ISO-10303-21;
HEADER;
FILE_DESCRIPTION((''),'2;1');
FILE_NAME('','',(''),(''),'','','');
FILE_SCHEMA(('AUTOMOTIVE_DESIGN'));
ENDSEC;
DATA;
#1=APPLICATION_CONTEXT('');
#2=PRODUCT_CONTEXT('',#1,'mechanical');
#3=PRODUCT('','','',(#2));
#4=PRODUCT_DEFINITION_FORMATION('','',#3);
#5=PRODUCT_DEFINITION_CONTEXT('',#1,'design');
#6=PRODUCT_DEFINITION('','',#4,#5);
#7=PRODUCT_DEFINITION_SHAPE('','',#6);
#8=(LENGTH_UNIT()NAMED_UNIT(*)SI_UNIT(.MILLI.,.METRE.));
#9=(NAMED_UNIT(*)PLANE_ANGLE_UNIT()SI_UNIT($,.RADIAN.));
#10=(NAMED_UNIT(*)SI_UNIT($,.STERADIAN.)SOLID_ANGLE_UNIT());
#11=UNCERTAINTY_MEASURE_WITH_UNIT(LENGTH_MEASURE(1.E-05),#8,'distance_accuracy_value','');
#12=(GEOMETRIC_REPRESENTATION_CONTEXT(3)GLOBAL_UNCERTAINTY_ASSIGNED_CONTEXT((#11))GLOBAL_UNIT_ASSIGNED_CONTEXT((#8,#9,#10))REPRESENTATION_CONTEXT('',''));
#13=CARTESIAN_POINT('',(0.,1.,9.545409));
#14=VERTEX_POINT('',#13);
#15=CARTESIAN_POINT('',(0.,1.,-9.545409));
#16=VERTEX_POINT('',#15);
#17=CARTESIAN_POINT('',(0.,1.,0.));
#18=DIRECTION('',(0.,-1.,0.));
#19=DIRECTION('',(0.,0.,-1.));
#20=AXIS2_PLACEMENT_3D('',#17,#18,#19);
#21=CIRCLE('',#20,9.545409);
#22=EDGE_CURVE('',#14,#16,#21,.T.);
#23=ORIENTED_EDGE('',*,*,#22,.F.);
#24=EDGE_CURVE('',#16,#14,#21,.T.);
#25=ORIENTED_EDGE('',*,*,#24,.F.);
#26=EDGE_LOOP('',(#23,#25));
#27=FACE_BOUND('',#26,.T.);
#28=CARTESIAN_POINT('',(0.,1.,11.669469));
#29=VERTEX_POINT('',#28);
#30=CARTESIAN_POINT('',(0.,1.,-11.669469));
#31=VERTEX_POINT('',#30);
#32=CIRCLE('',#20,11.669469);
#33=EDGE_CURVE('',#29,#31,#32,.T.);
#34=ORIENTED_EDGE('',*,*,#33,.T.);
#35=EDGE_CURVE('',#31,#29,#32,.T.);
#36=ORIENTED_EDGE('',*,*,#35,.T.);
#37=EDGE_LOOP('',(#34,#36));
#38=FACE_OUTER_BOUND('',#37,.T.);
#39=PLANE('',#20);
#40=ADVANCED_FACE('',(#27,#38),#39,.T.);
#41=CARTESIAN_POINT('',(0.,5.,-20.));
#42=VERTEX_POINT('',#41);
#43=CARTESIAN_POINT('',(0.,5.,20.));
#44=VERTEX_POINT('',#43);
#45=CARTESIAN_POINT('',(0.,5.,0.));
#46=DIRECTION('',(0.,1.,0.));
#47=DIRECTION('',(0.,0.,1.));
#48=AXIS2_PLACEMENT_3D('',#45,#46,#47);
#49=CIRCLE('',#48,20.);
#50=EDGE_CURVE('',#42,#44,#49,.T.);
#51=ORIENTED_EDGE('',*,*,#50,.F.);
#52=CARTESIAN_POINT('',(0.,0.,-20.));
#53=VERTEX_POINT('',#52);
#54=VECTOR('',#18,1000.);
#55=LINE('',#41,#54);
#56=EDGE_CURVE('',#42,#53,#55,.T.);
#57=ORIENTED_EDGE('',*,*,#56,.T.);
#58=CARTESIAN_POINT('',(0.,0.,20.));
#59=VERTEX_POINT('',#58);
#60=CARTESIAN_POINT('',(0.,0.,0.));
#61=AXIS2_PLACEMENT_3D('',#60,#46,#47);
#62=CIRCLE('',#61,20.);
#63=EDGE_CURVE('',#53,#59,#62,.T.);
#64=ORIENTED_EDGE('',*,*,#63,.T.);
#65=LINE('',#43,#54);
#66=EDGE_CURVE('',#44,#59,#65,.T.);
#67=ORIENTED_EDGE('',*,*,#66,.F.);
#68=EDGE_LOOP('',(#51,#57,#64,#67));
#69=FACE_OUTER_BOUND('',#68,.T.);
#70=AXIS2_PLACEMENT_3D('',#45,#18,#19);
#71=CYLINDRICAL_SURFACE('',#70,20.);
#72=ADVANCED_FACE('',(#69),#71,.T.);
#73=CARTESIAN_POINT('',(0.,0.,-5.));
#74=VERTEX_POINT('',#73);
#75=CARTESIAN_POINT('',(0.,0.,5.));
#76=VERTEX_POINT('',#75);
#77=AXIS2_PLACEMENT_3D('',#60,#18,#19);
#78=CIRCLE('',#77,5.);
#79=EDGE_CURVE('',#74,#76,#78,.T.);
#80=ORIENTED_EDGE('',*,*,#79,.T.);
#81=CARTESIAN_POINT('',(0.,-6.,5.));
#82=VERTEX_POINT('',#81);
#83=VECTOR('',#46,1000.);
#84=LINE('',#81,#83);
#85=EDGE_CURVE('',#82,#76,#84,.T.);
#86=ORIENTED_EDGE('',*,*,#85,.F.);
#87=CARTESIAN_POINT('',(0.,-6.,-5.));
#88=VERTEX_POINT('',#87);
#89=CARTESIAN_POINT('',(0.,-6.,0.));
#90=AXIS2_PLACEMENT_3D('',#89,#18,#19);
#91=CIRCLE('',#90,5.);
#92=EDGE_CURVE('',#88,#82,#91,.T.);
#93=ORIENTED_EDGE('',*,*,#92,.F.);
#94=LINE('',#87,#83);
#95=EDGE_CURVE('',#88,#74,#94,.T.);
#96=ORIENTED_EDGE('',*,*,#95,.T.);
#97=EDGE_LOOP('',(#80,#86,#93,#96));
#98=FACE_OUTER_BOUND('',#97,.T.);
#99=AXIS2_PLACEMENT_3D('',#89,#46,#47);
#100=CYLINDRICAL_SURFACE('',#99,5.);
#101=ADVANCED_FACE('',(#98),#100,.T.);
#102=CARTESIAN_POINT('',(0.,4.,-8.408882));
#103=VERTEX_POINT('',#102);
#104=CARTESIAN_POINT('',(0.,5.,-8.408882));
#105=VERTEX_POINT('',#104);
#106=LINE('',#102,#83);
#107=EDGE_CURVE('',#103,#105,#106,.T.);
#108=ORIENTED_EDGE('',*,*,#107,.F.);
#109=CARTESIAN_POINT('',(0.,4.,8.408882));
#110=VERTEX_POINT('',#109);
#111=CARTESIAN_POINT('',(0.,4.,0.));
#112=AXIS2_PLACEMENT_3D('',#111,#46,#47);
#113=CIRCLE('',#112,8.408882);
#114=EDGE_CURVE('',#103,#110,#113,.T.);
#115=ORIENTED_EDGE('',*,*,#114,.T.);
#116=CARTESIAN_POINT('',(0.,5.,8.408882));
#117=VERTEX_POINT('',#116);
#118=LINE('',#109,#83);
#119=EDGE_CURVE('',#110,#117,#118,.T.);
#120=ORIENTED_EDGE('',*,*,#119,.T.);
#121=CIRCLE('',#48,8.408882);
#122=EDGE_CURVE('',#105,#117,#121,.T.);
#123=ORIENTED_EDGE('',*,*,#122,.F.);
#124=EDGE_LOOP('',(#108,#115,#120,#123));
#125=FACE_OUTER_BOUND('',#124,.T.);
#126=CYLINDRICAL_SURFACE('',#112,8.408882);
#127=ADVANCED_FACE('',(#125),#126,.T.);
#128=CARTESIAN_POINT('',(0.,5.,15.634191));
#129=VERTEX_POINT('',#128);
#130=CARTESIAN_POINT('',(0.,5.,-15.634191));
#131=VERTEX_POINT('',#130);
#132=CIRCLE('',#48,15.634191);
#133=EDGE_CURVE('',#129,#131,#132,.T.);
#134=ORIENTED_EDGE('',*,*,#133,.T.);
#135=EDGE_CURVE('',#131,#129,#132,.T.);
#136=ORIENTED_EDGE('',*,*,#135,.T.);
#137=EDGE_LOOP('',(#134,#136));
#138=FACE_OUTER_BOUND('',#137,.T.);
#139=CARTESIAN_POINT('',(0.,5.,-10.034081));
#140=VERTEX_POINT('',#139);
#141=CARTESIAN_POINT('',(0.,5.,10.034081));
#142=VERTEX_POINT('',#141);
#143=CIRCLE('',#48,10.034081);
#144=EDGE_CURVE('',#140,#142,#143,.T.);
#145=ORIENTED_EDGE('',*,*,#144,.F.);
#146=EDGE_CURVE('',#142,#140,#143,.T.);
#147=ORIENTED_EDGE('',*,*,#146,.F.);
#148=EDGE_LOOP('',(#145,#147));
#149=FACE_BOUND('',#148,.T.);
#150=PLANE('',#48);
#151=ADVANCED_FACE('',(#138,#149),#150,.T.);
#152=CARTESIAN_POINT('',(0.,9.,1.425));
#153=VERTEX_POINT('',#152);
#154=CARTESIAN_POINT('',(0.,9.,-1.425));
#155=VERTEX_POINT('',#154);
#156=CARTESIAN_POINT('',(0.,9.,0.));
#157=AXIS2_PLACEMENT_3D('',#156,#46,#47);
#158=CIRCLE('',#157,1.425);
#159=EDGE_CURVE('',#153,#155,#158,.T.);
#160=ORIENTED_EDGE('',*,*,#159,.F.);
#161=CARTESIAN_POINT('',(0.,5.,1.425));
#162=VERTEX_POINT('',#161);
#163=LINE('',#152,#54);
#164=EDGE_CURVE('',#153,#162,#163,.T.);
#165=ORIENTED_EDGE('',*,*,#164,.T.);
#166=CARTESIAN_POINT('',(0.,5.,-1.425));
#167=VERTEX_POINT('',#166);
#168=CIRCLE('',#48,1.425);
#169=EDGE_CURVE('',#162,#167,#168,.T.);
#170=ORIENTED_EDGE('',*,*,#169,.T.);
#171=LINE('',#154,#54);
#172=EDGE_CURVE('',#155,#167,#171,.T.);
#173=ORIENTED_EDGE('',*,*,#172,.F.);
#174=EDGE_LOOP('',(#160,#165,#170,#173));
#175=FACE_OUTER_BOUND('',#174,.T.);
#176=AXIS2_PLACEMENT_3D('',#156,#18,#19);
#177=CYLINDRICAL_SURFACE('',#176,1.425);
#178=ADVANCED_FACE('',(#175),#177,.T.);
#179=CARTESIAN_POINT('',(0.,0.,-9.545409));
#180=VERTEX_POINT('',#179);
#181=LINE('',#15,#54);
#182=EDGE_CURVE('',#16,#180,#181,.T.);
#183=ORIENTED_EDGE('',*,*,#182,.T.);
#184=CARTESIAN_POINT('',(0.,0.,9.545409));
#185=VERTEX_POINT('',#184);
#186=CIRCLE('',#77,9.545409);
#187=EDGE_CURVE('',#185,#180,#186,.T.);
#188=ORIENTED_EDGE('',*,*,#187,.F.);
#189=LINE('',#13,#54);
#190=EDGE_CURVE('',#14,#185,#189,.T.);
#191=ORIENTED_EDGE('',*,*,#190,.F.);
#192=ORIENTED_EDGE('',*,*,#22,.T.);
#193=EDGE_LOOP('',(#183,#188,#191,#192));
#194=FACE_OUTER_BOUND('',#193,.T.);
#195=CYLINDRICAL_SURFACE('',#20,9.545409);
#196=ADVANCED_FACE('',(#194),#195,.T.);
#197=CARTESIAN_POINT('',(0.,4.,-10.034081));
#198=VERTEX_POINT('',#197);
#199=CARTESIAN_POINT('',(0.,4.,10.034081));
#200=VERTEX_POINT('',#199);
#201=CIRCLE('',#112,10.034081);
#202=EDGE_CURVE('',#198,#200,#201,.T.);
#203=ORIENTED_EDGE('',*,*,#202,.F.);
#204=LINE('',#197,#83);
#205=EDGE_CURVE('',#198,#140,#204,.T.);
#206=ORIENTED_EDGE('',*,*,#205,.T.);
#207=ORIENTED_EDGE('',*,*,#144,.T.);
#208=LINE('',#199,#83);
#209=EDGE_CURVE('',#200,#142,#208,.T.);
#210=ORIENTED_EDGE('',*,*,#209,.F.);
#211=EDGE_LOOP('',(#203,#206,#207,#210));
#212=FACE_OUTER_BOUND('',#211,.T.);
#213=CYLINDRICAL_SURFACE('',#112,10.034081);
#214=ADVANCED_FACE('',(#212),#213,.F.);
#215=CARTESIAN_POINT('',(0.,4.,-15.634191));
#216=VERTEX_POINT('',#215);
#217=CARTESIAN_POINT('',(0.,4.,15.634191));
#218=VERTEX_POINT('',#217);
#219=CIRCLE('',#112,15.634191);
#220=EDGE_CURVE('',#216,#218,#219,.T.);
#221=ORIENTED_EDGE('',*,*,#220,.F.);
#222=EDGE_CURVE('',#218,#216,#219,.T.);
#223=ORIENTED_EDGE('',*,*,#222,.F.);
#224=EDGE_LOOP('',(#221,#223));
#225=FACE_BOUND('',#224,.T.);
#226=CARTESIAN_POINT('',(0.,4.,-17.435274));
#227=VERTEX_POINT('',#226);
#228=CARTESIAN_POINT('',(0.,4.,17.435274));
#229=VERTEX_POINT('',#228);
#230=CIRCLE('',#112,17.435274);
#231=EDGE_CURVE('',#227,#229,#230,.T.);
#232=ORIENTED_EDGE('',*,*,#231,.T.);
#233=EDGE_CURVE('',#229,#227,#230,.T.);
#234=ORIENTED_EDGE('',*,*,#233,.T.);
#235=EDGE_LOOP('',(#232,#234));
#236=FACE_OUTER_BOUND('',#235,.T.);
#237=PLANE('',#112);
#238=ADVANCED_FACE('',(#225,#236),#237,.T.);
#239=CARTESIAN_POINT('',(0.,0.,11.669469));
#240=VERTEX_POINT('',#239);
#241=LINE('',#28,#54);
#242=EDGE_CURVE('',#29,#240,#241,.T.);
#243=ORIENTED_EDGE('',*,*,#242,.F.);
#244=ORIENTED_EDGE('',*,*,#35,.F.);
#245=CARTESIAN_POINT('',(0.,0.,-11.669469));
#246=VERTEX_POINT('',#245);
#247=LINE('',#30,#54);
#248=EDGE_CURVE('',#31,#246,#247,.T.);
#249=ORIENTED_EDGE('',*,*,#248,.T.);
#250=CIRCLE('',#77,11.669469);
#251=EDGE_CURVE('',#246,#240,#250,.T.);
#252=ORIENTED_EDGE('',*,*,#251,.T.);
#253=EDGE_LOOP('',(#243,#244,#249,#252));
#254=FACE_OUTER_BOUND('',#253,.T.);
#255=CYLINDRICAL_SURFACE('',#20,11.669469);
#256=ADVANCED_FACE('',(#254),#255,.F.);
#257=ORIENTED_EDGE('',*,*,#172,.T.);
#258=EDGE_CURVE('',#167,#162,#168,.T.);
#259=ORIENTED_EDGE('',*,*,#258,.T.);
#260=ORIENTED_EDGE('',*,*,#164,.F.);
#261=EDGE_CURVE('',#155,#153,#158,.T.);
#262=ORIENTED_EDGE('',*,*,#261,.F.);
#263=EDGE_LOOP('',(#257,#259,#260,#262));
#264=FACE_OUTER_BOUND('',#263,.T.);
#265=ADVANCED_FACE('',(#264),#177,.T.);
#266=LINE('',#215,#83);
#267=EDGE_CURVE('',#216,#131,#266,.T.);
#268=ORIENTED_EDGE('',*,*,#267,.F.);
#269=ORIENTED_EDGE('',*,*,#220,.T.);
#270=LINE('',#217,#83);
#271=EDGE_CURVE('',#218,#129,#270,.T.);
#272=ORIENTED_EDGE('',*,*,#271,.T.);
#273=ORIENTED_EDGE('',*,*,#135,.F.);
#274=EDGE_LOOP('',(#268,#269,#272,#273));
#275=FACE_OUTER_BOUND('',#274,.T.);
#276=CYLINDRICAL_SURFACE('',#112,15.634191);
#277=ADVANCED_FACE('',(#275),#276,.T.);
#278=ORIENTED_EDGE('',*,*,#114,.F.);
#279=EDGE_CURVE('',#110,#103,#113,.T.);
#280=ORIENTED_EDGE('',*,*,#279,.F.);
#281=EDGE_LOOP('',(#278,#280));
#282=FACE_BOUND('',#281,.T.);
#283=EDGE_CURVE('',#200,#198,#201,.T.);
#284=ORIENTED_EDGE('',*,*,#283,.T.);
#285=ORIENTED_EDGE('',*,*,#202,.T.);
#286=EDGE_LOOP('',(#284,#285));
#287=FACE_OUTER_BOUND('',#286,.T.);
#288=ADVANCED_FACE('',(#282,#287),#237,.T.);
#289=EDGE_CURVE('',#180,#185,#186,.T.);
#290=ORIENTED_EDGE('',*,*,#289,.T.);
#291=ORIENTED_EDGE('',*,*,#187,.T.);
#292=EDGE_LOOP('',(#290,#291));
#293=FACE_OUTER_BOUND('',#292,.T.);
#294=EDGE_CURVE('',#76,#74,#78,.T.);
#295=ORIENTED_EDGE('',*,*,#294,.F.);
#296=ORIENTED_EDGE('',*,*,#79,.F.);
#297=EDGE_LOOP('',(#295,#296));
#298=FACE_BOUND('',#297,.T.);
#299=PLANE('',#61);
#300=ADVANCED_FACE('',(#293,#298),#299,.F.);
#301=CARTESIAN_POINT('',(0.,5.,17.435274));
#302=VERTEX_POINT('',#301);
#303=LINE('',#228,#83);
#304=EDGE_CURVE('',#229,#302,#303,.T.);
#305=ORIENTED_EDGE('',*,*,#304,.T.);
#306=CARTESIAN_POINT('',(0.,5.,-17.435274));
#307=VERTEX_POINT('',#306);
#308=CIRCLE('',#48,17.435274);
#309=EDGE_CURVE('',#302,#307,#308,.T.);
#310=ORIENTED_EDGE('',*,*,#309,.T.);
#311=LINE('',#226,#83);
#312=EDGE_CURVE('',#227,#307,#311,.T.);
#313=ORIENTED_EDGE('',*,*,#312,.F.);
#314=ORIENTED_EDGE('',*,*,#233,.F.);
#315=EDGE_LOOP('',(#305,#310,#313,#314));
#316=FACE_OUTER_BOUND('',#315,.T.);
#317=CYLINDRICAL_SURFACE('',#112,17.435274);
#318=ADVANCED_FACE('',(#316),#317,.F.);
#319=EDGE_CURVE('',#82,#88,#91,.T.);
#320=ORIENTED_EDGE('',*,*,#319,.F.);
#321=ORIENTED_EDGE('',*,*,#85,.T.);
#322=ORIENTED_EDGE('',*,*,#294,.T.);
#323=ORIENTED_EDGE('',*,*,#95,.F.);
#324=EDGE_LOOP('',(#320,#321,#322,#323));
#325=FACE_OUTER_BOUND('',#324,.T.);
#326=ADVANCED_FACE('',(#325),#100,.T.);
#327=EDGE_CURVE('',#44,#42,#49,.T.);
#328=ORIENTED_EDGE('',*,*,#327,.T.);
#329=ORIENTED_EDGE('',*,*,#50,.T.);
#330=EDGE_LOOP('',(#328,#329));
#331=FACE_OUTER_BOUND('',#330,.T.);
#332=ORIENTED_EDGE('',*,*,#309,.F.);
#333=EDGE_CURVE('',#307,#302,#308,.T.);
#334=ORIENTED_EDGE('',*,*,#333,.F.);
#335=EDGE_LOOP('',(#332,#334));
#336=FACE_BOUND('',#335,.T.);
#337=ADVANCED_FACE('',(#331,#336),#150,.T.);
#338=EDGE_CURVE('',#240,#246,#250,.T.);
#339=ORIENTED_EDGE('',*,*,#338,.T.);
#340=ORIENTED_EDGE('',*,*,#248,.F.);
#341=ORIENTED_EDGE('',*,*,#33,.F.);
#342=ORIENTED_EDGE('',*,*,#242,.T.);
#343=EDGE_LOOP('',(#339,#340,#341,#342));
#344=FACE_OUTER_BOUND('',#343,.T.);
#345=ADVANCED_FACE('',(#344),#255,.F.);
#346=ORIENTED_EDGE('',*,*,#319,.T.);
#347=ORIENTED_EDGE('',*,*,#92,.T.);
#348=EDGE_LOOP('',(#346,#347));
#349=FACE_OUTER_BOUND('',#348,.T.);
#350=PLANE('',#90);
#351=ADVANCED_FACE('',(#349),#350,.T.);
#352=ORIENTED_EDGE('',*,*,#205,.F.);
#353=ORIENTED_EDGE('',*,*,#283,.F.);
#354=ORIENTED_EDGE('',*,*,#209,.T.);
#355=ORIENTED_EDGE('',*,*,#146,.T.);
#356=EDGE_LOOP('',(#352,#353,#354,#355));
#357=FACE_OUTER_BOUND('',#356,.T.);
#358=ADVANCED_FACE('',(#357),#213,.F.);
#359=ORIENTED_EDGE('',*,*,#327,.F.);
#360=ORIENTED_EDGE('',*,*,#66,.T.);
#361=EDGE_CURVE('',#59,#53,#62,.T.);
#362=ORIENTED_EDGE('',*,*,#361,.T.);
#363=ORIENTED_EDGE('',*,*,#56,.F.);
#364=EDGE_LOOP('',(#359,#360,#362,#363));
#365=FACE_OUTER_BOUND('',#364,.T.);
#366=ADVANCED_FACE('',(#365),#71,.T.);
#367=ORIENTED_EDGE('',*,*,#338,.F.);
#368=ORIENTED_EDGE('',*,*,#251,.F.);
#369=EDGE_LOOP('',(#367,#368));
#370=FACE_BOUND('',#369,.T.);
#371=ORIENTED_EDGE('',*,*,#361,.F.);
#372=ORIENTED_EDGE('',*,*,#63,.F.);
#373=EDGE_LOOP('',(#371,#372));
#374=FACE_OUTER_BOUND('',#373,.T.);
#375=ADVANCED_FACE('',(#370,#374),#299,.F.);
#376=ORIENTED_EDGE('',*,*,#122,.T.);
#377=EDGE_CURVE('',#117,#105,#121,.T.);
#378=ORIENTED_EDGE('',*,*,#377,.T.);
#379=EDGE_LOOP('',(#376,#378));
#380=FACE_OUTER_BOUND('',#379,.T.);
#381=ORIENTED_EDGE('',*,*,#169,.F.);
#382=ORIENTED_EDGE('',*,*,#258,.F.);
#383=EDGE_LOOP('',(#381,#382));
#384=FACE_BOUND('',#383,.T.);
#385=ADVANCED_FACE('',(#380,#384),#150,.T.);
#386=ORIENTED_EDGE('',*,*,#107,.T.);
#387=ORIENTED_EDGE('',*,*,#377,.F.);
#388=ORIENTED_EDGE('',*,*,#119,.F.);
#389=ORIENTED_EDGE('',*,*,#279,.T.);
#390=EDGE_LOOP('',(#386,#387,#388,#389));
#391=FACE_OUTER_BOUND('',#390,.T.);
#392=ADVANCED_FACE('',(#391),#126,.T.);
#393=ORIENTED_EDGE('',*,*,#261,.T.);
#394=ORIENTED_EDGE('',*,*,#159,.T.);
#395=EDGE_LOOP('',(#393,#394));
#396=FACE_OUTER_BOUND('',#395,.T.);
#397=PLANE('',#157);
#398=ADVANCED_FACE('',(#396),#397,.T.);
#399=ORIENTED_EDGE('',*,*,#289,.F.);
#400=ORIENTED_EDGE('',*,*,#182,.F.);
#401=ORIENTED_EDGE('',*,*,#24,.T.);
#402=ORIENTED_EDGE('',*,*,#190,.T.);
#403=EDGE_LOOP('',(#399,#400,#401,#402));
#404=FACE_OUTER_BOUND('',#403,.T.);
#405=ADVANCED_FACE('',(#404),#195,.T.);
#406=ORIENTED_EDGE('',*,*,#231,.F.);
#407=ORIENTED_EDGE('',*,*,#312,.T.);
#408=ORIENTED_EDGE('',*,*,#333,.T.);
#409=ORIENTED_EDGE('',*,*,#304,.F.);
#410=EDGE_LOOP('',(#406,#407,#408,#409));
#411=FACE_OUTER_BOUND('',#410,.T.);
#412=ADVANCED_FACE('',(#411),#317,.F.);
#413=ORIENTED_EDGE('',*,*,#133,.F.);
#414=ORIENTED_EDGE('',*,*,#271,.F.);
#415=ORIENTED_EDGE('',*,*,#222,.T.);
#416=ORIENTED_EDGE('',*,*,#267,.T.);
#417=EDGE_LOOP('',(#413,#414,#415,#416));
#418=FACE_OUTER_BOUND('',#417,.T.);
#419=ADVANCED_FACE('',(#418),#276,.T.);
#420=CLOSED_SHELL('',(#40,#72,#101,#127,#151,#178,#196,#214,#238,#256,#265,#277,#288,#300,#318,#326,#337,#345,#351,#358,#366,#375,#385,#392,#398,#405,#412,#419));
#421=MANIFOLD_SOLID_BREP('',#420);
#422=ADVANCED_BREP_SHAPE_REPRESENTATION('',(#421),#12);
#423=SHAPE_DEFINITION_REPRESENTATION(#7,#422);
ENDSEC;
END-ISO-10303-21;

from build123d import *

# Parameters (mm, degrees)
SKETCH_1_R          = 20
EXTRUDE_1_DEPTH     = 5
SKETCH_2_R          = 5
EXTRUDE_2_DEPTH     = 6
SKETCH_3_R          = 11.669468733
SKETCH_3_R_2        = 9.545408708
CUT_EXTRUDE_1_DEPTH = 1
SKETCH_4_R          = 1.425
EXTRUDE_3_DEPTH     = 4
SKETCH_5_R          = 17.435273898
SKETCH_5_R_2        = 15.634190673
CUT_EXTRUDE_2_DEPTH = 1
SKETCH_6_R          = 10.034081131
SKETCH_6_R_2        = 8.408881881
CUT_EXTRUDE_3_DEPTH = 1


with BuildPart() as part:
    # 草图1 → 凸台-拉伸1 (new body)
    with BuildSketch(Plane(origin=(0, 0, 0), x_dir=(1, 0, 0), z_dir=(0, 1, 0))):
        with Locations(Location((0, 0, 0), (0, 0, 270))):
            Circle(SKETCH_1_R)
    extrude(amount=EXTRUDE_1_DEPTH)

    # 草图2 → 凸台-拉伸2 (add)
    with BuildSketch(Plane.XZ):
        with Locations(Location((0, 0, 0), (0, 0, 270))):
            Circle(SKETCH_2_R)
    extrude(amount=EXTRUDE_2_DEPTH)

    # 草图3 → 切除-拉伸1 (cut)
    with BuildSketch(Plane.XZ):
        with Locations(Location((0, 0, 0), (0, 0, 270))):
            Circle(SKETCH_3_R)
        with Locations(Location((0, 0, 0), (0, 0, 270))):
            Circle(SKETCH_3_R_2, mode=Mode.SUBTRACT)
    extrude(amount=-CUT_EXTRUDE_1_DEPTH, mode=Mode.SUBTRACT)

    # 草图4 → 凸台-拉伸3 (add)
    with BuildSketch(Plane(origin=(0, 5, 0), x_dir=(1, 0, 0), z_dir=(0, 1, 0))):
        with Locations(Location((0, 0, 0), (0, 0, 270))):
            Circle(SKETCH_4_R)
    extrude(amount=EXTRUDE_3_DEPTH)

    # 草图5 → 切除-拉伸2 (cut)
    with BuildSketch(Plane(origin=(0, 5, 0), x_dir=(1, 0, 0), z_dir=(0, 1, 0))):
        with Locations(Location((0, 0, 0), (0, 0, 270))):
            Circle(SKETCH_5_R)
        with Locations(Location((0, 0, 0), (0, 0, 270))):
            Circle(SKETCH_5_R_2, mode=Mode.SUBTRACT)
    extrude(amount=-CUT_EXTRUDE_2_DEPTH, mode=Mode.SUBTRACT)

    # 草图6 → 切除-拉伸3 (cut)
    with BuildSketch(Plane(origin=(0, 5, 0), x_dir=(1, 0, 0), z_dir=(0, 1, 0))):
        with Locations(Location((0, 0, 0), (0, 0, 270))):
            Circle(SKETCH_6_R)
        with Locations(Location((0, 0, 0), (0, 0, 270))):
            Circle(SKETCH_6_R_2, mode=Mode.SUBTRACT)
    extrude(amount=-CUT_EXTRUDE_3_DEPTH, mode=Mode.SUBTRACT)


solid = part.part
